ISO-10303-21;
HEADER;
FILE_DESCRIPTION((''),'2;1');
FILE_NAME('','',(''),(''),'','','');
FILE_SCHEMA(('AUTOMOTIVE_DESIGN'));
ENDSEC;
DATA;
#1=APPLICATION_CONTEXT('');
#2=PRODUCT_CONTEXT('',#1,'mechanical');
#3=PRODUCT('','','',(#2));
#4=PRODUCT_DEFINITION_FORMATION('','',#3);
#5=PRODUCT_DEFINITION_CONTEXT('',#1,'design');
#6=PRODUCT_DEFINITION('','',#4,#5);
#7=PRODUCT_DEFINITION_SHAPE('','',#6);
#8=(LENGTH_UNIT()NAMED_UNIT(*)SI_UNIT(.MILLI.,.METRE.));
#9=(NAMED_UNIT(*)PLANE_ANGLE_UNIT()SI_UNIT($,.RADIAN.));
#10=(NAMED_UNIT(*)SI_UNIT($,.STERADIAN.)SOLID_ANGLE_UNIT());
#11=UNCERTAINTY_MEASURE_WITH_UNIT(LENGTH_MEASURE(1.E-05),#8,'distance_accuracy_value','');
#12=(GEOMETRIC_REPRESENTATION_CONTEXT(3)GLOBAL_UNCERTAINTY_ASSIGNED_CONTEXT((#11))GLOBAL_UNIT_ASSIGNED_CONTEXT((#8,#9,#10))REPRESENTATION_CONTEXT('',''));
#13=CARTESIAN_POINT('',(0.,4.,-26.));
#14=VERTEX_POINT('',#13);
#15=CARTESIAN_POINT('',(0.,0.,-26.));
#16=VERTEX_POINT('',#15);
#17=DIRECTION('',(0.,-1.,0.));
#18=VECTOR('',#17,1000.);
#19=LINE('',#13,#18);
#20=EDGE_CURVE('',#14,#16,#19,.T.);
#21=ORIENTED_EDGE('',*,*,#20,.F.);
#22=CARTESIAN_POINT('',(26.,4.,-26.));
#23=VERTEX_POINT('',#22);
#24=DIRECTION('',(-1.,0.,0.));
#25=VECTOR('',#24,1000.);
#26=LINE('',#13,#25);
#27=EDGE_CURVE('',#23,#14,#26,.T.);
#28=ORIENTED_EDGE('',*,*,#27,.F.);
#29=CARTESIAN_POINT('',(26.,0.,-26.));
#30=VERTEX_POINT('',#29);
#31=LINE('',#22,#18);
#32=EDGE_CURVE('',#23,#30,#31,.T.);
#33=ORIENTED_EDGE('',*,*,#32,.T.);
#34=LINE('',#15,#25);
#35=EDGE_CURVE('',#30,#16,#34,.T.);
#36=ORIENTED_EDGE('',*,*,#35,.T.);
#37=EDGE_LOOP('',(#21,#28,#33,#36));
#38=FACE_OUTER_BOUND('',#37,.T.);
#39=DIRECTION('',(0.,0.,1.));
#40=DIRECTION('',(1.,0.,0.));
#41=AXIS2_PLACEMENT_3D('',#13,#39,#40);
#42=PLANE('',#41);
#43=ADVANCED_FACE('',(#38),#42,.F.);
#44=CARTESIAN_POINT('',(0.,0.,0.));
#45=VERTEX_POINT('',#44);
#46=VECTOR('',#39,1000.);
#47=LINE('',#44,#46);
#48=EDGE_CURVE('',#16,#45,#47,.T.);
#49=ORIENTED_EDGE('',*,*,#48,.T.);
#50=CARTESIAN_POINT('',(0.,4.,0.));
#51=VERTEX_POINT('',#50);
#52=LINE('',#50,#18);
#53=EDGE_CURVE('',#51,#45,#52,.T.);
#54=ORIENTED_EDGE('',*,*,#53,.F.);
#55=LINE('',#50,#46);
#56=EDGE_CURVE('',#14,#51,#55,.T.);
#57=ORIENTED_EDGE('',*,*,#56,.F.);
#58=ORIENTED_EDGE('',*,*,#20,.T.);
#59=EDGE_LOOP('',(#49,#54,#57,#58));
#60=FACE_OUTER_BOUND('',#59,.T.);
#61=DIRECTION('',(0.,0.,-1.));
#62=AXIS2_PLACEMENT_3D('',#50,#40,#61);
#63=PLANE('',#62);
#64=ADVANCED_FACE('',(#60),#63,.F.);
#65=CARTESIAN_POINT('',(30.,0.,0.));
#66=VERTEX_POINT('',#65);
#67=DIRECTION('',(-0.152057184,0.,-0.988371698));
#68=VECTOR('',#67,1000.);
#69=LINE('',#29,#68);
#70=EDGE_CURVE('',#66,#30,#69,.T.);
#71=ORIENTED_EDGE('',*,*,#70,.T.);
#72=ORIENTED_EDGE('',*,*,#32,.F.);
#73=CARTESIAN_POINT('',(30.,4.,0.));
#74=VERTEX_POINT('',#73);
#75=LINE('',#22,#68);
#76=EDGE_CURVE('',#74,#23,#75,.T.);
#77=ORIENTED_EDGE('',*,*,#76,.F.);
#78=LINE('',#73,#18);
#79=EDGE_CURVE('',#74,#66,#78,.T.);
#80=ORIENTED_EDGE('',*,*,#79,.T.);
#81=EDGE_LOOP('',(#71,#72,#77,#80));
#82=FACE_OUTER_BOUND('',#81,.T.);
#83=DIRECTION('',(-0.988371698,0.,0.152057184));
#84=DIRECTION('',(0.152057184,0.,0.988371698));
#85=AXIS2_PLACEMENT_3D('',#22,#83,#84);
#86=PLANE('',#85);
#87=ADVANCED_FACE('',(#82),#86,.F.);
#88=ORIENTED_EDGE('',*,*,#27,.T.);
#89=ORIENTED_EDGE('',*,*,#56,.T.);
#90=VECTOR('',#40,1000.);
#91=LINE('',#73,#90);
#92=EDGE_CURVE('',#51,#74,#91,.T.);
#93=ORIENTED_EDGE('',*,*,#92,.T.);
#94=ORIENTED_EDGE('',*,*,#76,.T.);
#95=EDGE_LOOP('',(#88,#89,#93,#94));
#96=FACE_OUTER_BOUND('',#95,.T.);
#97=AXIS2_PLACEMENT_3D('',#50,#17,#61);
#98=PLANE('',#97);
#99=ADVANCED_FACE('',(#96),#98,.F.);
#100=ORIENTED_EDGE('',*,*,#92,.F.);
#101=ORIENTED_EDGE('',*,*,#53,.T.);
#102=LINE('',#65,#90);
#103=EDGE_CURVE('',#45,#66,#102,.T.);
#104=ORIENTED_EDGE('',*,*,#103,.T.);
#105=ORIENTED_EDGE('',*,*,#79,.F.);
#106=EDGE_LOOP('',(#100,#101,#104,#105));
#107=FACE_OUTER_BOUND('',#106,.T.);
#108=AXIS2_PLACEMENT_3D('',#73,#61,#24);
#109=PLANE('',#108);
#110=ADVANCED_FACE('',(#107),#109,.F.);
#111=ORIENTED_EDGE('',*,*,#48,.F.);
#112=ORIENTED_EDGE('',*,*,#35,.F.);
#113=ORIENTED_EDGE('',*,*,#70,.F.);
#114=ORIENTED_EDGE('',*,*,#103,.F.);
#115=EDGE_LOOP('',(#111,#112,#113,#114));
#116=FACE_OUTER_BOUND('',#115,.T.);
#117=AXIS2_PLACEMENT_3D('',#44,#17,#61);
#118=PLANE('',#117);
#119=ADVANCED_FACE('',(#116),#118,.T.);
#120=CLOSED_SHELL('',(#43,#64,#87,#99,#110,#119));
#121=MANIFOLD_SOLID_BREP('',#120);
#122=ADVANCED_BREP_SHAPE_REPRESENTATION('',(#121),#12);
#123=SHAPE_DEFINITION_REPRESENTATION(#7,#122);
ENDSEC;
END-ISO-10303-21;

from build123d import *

# Parameters (mm, degrees)
EXTRUDE_1_DEPTH = 4


with BuildPart() as part:
    # 草图1 → 凸台-拉伸1 (new body)
    with BuildSketch(Plane(origin=(0, 0, 0), x_dir=(1, 0, 0), z_dir=(0, 1, 0))):
        Polygon((0, 0), (0, 26), (26, 26), (30, 0), align=None)
    extrude(amount=EXTRUDE_1_DEPTH)


solid = part.part
